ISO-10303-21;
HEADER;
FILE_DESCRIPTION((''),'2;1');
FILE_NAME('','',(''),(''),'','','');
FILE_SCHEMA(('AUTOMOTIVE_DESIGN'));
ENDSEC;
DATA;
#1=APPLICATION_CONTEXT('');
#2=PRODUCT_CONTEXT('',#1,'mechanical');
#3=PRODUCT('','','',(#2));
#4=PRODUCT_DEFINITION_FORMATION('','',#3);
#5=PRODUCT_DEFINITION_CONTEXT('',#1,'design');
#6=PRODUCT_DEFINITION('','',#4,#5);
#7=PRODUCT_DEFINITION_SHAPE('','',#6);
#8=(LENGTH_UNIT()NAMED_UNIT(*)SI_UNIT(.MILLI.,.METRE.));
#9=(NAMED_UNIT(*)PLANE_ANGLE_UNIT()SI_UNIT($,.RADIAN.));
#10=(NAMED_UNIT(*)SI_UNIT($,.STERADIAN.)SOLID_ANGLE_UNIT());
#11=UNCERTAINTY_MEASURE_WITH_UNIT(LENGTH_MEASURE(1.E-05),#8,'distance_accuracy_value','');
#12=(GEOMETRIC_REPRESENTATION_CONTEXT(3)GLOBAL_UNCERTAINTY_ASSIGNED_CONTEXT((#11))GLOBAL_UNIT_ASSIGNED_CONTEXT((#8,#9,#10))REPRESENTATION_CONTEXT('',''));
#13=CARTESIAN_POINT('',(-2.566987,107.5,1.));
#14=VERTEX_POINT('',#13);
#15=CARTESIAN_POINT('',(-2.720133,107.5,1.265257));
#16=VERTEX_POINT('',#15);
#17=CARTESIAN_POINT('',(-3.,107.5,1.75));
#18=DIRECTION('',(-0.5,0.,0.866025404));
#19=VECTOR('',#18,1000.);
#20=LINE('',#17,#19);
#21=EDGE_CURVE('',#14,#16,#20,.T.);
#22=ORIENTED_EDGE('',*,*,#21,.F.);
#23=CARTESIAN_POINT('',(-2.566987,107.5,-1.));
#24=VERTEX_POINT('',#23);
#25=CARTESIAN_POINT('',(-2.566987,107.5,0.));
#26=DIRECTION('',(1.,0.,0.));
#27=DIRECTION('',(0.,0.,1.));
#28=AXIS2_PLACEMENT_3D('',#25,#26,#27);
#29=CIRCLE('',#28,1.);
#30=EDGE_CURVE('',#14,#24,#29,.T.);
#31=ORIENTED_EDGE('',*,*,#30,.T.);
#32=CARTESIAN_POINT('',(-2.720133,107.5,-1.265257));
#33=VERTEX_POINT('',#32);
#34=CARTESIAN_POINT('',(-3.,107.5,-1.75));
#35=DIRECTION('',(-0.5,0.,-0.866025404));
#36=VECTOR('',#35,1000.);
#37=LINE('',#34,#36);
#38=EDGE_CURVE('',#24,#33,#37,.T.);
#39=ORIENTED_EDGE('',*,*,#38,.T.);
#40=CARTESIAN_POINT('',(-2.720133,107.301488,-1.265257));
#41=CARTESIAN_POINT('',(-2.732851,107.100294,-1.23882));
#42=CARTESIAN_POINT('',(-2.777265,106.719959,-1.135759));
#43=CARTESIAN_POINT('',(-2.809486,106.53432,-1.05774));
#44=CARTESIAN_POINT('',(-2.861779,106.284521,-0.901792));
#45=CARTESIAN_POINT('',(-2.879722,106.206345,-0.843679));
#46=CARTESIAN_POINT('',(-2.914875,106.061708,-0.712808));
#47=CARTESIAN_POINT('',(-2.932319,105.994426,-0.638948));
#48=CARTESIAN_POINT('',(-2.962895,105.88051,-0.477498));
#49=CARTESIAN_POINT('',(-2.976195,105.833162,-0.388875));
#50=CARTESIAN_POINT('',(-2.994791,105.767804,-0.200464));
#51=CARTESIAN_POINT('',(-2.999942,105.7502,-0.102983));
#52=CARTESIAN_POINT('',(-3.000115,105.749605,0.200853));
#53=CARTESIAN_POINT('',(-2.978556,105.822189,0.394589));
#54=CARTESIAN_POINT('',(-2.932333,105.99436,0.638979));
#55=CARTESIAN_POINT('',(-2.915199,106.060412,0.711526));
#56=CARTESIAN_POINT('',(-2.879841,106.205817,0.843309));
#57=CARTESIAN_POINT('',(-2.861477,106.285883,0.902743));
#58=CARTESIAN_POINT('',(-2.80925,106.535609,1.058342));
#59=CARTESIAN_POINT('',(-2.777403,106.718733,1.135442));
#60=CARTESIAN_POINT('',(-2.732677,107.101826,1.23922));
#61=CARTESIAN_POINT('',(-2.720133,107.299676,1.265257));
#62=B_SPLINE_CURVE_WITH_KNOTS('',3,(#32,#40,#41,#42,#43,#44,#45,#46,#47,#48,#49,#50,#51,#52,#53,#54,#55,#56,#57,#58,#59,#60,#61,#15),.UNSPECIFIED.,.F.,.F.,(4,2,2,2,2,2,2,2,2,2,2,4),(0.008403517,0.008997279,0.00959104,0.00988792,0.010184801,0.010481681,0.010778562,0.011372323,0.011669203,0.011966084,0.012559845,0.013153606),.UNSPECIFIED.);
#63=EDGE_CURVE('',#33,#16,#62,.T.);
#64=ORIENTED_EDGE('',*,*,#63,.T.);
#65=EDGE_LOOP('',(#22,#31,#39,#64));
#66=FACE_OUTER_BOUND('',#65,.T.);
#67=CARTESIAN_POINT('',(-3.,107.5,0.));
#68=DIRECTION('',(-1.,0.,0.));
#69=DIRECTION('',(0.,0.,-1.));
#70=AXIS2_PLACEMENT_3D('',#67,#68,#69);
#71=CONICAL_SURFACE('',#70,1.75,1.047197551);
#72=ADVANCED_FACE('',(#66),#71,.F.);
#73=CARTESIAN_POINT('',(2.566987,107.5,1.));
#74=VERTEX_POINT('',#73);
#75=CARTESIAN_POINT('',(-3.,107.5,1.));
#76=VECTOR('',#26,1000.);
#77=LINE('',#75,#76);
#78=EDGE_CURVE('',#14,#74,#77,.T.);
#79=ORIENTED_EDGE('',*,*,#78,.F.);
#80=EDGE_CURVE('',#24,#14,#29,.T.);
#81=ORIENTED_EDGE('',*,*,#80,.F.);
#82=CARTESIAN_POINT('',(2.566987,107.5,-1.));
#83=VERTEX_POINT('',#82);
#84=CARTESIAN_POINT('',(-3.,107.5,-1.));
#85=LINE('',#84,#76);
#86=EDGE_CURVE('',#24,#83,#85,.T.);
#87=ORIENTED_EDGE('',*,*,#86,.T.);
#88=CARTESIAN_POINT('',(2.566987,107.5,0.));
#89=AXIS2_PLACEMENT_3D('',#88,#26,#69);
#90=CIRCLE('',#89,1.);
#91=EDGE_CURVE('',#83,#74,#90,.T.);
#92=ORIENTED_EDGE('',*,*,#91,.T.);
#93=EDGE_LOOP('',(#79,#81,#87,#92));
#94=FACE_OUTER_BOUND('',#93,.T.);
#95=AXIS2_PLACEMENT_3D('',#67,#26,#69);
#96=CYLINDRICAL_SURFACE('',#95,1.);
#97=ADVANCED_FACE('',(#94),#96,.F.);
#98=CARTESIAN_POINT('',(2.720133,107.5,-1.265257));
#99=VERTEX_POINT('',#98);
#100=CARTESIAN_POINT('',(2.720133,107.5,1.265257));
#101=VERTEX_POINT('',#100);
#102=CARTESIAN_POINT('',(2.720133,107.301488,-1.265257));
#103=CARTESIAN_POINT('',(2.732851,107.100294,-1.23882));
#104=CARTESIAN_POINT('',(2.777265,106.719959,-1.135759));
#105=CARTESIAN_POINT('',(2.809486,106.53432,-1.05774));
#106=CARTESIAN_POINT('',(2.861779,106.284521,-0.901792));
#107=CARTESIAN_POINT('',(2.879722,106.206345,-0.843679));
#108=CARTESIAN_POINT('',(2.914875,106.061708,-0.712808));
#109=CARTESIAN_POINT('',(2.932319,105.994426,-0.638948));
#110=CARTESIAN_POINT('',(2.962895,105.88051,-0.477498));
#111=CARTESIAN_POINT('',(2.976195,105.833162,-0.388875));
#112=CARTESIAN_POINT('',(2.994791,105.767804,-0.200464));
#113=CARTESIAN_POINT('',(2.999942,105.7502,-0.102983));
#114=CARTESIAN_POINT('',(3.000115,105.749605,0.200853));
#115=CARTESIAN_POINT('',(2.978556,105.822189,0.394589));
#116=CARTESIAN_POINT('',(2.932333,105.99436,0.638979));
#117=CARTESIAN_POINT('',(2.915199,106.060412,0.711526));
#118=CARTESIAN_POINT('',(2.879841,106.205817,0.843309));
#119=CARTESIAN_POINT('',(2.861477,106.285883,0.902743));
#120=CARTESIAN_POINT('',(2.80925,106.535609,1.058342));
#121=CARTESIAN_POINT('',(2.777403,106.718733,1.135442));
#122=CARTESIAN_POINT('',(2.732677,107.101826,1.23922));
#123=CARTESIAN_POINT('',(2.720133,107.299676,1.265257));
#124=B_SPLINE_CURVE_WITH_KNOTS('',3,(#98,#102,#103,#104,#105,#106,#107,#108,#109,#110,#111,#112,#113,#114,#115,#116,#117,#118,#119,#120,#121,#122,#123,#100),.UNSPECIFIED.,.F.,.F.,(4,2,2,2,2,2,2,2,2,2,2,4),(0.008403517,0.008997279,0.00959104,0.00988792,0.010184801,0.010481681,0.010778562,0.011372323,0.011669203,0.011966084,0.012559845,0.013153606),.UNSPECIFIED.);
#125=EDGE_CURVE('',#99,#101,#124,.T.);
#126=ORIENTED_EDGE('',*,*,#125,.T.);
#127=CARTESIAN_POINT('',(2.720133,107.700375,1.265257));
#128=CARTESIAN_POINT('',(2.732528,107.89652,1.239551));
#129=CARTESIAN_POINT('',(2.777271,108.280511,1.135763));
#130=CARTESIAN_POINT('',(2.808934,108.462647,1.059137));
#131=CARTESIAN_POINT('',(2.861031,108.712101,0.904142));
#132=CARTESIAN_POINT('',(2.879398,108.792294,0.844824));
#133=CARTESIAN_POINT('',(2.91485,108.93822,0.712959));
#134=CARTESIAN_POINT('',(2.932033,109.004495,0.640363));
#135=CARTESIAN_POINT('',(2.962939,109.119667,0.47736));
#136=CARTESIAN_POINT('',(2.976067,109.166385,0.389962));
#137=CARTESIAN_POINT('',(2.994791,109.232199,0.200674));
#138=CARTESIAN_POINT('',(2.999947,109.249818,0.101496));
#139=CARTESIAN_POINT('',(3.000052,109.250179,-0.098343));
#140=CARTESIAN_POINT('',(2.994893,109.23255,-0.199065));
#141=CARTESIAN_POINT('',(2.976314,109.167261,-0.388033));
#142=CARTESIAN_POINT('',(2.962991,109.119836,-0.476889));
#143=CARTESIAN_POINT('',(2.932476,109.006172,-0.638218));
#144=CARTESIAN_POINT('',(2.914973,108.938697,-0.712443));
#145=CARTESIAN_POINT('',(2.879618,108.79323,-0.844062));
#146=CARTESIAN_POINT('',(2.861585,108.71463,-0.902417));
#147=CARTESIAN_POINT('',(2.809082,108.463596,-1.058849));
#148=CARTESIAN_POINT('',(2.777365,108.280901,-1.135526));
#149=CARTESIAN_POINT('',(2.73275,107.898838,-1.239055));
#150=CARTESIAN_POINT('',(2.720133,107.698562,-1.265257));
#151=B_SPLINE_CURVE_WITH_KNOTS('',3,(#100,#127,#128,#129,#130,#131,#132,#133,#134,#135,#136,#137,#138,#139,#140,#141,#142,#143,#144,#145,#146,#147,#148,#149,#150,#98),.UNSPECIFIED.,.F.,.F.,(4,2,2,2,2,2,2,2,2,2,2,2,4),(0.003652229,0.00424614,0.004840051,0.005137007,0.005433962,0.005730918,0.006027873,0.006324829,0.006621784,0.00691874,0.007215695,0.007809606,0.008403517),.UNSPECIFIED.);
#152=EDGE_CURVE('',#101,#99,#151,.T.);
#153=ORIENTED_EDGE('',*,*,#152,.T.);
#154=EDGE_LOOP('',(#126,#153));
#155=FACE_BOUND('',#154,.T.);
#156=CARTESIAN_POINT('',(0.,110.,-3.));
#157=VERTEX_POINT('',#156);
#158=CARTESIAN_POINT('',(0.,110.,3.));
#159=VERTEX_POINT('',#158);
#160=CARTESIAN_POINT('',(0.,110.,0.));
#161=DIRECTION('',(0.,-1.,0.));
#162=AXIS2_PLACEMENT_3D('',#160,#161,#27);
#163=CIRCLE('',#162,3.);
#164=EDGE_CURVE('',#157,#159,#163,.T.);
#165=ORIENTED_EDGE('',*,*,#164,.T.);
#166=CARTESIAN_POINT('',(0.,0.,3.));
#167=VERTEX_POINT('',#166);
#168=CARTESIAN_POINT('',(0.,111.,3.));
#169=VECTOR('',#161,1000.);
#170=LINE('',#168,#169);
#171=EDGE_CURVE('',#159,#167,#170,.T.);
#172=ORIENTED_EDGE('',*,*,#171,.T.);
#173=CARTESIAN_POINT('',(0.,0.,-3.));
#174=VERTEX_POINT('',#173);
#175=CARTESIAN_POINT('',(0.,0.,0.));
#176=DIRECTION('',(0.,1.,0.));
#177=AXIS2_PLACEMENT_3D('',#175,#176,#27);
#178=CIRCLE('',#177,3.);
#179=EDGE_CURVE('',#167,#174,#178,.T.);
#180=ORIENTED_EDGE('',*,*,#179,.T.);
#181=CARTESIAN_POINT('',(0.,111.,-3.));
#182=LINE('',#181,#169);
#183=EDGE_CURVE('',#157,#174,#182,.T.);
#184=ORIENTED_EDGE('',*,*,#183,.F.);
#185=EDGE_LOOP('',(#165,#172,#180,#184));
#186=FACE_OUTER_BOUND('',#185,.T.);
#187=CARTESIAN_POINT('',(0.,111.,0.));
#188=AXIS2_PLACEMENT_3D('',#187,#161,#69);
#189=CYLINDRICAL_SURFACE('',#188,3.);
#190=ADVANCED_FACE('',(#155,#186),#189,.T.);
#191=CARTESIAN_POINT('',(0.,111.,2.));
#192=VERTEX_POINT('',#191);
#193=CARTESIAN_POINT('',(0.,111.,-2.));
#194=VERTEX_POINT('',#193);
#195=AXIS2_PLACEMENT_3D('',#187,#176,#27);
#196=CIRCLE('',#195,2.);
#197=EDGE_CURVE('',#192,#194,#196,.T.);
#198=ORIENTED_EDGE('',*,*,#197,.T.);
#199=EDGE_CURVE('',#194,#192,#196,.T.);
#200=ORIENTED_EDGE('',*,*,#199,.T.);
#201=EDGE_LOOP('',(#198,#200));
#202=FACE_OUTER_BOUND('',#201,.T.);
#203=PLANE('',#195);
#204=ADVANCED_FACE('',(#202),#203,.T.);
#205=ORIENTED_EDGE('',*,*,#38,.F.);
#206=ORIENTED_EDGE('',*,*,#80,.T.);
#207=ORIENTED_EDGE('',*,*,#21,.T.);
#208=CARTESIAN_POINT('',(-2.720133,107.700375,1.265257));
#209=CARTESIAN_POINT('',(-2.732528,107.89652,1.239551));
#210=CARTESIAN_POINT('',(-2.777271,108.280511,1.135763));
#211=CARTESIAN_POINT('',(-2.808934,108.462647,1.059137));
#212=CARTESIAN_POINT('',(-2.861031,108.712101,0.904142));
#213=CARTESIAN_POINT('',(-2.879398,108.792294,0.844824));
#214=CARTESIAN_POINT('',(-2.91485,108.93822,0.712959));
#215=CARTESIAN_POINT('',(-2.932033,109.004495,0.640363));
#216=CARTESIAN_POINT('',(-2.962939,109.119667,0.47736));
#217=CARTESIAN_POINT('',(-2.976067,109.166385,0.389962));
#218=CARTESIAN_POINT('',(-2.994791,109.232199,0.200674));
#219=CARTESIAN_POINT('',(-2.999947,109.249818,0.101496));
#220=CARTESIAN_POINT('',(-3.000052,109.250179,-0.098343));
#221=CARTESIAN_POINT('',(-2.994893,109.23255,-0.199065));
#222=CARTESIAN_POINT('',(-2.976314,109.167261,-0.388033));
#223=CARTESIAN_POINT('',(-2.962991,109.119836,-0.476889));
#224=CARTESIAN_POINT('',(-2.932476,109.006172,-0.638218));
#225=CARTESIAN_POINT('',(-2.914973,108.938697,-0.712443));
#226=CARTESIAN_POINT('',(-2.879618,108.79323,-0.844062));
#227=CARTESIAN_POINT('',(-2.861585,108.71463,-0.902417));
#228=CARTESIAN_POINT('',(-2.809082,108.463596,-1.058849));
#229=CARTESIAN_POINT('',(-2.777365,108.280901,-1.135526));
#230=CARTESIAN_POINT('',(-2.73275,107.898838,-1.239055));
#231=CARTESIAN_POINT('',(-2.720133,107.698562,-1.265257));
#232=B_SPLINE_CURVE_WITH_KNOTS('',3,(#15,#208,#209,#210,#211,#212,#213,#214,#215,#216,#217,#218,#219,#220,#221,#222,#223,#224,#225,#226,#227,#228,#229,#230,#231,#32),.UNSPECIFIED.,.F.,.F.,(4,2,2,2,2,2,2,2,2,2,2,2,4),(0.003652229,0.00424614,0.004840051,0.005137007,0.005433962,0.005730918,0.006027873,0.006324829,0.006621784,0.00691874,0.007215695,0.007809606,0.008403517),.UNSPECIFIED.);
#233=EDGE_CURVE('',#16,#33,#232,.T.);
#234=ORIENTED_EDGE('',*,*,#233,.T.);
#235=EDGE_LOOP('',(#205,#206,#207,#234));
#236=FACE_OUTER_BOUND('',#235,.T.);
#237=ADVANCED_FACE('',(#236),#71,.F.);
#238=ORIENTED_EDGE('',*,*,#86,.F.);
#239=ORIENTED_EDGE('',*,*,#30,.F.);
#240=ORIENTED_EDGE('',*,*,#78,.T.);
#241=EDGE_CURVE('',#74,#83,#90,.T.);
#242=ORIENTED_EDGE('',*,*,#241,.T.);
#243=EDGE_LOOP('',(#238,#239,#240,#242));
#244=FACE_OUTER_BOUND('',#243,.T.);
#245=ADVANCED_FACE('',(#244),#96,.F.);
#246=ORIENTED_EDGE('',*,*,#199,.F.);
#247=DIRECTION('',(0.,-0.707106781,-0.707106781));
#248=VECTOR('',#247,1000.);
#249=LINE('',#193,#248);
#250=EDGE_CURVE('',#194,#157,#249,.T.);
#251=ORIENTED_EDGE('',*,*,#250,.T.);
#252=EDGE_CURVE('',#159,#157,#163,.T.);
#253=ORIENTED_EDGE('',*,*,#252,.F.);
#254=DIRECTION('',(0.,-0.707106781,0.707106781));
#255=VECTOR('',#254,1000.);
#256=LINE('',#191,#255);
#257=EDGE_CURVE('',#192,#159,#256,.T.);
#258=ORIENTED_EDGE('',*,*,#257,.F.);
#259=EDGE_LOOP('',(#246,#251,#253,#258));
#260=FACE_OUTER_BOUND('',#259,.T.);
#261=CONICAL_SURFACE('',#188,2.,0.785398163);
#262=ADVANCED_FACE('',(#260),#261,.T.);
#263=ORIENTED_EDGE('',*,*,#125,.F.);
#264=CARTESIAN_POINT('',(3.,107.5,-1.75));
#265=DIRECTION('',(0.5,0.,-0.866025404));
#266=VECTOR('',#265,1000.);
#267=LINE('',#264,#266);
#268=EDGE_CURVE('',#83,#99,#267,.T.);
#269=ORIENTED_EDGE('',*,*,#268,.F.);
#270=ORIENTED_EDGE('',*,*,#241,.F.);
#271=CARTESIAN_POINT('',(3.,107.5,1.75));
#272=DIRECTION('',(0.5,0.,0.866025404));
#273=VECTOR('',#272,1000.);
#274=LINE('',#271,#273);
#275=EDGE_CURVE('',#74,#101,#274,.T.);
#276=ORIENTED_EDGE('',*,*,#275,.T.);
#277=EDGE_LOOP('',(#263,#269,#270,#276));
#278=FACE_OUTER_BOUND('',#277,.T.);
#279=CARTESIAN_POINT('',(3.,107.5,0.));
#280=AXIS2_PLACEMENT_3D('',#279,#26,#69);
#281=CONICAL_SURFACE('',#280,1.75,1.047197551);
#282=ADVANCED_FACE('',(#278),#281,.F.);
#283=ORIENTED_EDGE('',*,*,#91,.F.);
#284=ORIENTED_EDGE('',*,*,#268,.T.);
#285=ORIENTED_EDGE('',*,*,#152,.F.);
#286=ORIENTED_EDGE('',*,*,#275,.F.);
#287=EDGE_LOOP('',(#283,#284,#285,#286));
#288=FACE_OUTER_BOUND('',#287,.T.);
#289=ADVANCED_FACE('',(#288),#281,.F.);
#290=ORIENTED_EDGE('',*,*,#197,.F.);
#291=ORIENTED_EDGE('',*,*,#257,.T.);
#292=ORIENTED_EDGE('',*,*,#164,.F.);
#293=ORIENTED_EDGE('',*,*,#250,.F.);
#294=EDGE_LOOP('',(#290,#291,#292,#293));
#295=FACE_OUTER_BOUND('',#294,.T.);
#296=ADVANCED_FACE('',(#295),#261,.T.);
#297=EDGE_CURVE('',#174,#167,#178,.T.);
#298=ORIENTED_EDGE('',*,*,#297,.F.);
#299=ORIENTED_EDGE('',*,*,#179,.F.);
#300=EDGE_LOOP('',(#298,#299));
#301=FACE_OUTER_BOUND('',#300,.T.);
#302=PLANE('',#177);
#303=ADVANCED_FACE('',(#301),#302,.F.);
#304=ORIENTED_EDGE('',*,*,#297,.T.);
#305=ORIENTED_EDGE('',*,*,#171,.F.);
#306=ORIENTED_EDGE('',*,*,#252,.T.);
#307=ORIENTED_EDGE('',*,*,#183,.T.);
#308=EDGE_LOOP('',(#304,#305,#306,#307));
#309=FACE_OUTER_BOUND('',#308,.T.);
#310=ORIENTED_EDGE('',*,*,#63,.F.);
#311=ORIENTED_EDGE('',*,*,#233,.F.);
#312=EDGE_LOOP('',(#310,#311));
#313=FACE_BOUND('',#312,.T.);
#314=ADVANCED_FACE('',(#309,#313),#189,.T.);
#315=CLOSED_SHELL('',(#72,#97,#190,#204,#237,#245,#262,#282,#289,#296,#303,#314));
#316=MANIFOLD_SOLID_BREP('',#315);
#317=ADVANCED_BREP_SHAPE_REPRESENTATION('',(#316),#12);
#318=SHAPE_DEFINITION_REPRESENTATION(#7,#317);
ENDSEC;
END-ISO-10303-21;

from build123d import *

# Parameters (mm, degrees)
SKETCH1_R               = 3
BOSS_EXTRUDE1_DEPTH     = 111
CUT_EXTRUDE1_DEPTH      = 112.081051489
CUT_EXTRUDE1_DEPTH_BACK = 112.081051489
SKETCH2_R               = 1
CHAMFER3_SIZE           = 1


with BuildPart() as part:
    # Sketch1 → Boss-Extrude1 (new body)
    with BuildSketch(Plane(origin=(0, 0, 0), x_dir=(1, 0, 0), z_dir=(0, 1, 0))):
        with Locations(Location((0, 0, 0), (0, 0, 270))):
            Circle(SKETCH1_R)
    extrude(amount=BOSS_EXTRUDE1_DEPTH)

    # Sketch2 → Cut-Extrude1 (cut, two sides: drawn at the far end of the back side and taken through both)
    with BuildSketch(Plane(origin=(0, 0, 0), x_dir=(0, 0, -1), z_dir=(1, 0, 0)).offset(-CUT_EXTRUDE1_DEPTH_BACK)):
        with Locations((0, 107.5)):
            Circle(SKETCH2_R)
    extrude(amount=CUT_EXTRUDE1_DEPTH + CUT_EXTRUDE1_DEPTH_BACK, mode=Mode.SUBTRACT)

    # Cut-Extrude2 cone 1 section (through the dimple's axis) → Cut-Extrude2 (revolve, cut)
    with BuildSketch(Plane(origin=(3, 107.5, 0), x_dir=(0, 0, -1), z_dir=(0, 1, 0))):
        Polygon((0, 0), (1.75, 0), (0, 1.010362971), align=None)
    cut_extrude2 = revolve(axis=Axis((3, 107.5, 0), (-1, 0, 0)), mode=Mode.SUBTRACT)

    # Mirror1: Cut-Extrude2 across plane
    add(cut_extrude2.mirror(Plane(origin=(0, 0, 0), x_dir=(0, 0, 1), z_dir=(1, 0, 0))), mode=Mode.SUBTRACT)

    # Chamfer3
    chamfer3_edges = [part.edges().sort_by_distance(p)[0] for p in [
        (0, 111, -3),
    ]]
    chamfer(chamfer3_edges, length=CHAMFER3_SIZE)


solid = part.part
